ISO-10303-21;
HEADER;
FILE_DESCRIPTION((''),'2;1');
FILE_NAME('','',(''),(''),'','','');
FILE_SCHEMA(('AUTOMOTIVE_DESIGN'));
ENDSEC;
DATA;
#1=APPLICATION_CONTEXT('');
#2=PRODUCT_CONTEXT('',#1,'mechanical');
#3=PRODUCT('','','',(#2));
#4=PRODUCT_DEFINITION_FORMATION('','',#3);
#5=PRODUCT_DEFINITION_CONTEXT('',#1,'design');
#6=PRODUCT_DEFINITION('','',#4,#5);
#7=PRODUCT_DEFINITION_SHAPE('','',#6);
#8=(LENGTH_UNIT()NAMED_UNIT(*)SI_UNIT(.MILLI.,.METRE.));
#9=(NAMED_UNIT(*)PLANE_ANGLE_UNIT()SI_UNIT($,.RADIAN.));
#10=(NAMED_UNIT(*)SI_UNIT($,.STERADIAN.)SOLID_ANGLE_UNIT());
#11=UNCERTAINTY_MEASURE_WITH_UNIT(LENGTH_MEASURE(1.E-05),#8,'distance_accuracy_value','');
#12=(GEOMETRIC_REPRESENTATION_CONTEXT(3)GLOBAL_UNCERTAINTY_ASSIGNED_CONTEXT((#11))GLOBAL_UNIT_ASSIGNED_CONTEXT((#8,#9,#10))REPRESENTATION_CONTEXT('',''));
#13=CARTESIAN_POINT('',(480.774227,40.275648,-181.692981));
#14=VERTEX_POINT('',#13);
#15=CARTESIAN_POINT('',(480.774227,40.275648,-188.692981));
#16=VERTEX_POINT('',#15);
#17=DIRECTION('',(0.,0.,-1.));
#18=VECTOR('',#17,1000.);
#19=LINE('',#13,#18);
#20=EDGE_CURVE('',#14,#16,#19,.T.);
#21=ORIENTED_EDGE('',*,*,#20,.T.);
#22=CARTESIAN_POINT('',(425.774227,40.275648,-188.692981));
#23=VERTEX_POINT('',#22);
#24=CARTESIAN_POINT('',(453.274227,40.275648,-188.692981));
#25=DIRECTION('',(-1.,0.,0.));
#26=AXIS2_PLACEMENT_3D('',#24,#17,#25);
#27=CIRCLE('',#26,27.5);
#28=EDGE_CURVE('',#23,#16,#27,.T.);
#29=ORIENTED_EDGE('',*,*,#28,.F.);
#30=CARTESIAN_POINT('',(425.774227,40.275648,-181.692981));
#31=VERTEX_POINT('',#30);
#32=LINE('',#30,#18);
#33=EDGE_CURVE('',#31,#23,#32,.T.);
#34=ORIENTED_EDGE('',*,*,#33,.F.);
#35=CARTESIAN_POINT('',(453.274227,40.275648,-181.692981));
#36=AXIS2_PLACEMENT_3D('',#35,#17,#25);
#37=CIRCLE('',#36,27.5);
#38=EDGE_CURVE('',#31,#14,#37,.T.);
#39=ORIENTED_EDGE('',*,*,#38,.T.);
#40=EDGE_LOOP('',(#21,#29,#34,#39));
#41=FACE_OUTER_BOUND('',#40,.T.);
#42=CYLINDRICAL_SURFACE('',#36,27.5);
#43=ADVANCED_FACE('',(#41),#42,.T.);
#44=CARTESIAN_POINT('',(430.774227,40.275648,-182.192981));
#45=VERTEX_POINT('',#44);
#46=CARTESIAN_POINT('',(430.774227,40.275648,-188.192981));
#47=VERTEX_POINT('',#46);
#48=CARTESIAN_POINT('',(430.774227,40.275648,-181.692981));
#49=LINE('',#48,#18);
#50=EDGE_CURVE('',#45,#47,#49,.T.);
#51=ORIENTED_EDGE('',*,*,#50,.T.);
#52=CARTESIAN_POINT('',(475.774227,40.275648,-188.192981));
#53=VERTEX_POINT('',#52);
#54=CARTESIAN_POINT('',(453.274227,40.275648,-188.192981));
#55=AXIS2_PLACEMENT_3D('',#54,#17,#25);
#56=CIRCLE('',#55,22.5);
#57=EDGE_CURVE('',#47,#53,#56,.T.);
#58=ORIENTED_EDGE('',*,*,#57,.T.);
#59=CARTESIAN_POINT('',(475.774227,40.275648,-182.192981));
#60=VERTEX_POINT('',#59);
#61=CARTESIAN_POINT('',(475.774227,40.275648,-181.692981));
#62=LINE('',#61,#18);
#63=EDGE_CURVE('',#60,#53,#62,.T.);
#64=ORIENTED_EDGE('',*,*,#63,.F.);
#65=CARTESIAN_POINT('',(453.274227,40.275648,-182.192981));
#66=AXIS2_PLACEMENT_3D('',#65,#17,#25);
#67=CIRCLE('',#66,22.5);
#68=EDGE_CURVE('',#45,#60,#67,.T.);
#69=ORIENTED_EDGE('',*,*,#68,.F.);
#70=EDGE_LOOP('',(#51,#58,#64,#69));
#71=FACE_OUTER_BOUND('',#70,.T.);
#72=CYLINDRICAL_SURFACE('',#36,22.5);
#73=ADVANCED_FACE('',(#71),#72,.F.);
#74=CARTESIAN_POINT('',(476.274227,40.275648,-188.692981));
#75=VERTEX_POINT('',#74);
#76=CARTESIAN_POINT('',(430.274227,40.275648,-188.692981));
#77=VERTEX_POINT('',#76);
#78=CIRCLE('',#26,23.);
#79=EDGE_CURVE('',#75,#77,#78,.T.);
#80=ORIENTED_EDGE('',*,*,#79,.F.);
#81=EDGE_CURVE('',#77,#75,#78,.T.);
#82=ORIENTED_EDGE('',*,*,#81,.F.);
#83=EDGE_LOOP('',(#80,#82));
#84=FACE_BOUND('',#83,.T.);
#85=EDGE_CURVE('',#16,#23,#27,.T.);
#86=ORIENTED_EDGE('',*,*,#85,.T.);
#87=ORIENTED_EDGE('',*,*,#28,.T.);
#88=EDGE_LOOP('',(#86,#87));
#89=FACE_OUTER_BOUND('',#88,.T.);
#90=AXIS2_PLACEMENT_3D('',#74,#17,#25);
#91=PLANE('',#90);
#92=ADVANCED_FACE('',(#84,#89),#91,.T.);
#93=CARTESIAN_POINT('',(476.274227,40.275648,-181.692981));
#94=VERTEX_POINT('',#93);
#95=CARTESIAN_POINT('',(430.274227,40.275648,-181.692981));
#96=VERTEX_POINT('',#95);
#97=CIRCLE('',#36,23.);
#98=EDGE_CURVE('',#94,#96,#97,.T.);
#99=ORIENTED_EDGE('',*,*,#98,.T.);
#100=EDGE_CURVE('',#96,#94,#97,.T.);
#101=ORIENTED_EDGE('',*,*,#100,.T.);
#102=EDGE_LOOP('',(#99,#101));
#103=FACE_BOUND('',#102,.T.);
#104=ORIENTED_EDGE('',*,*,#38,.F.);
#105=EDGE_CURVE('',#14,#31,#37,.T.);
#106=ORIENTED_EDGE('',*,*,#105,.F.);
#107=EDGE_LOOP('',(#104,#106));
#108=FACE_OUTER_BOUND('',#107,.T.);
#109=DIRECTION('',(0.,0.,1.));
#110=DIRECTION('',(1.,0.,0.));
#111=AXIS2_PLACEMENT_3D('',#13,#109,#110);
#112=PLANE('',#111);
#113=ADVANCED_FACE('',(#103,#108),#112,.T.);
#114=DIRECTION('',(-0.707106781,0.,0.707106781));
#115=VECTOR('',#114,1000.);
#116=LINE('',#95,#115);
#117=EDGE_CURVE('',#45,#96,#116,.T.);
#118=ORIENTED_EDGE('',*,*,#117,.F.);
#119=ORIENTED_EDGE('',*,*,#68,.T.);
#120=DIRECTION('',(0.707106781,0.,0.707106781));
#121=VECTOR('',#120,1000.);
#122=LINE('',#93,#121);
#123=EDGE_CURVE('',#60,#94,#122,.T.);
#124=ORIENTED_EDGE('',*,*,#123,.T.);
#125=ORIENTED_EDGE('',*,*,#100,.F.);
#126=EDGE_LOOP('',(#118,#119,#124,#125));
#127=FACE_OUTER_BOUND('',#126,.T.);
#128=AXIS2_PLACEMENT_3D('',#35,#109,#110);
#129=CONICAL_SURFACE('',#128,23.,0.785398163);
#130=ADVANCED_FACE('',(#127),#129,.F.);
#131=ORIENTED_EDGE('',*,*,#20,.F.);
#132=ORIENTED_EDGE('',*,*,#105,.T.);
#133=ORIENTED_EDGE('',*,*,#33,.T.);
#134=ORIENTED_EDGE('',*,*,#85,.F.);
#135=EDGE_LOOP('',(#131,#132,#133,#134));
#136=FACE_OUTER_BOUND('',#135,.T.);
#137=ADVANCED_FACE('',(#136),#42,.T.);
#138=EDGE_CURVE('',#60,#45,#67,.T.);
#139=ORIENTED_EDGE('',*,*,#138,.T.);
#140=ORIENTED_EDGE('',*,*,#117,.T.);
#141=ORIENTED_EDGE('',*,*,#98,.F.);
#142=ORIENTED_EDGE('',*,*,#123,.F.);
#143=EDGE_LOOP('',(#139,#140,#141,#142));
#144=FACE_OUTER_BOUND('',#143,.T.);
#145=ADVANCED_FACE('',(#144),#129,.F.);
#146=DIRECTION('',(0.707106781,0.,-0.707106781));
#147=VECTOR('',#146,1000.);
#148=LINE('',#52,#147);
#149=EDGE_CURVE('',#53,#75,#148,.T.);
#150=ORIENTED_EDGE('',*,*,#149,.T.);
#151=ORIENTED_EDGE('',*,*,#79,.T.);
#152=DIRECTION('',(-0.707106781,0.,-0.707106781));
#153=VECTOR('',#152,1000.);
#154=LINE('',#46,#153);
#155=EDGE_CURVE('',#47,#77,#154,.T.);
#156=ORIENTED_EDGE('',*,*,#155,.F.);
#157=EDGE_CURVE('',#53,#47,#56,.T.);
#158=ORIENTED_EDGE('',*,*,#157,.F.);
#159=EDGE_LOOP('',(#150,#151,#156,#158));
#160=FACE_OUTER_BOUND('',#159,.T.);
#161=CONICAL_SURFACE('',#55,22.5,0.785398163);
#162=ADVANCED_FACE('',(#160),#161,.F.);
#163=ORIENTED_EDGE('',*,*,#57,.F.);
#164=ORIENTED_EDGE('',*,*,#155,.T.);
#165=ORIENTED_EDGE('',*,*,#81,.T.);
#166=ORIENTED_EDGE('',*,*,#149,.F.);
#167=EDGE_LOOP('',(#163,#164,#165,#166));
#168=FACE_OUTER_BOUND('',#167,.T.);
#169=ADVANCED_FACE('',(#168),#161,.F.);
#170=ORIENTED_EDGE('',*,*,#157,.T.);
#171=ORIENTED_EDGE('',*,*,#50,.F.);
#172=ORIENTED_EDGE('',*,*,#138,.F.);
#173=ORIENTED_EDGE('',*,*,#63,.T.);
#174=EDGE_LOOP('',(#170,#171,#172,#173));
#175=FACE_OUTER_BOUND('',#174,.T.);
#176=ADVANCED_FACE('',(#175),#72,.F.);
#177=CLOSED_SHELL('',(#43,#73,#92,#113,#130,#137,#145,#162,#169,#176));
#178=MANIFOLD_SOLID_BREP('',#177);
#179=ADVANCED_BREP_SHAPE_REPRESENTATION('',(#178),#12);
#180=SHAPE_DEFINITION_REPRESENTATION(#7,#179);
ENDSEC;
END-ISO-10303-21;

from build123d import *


with BuildPart() as part:
    # Sketch1 → Revolve1 (revolve)
    with BuildSketch(Plane.XZ.offset(-40.2756484), mode=Mode.PRIVATE) as revolve1_sk:
        Polygon((475.77422742, -188.192981355), (476.27422742, -188.692981355), (480.77422742, -188.692981355), (480.77422742, -181.692981355), (476.27422742, -181.692981355), (475.77422742, -182.192981355), align=None)
    revolve(revolve1_sk.sketch.rotate(Axis((453.27422742, 40.2756484, -181.692981355), (0, 0, -1)), 180), axis=Axis((453.27422742, 40.2756484, -181.692981355), (0, 0, -1)))


solid = part.part
